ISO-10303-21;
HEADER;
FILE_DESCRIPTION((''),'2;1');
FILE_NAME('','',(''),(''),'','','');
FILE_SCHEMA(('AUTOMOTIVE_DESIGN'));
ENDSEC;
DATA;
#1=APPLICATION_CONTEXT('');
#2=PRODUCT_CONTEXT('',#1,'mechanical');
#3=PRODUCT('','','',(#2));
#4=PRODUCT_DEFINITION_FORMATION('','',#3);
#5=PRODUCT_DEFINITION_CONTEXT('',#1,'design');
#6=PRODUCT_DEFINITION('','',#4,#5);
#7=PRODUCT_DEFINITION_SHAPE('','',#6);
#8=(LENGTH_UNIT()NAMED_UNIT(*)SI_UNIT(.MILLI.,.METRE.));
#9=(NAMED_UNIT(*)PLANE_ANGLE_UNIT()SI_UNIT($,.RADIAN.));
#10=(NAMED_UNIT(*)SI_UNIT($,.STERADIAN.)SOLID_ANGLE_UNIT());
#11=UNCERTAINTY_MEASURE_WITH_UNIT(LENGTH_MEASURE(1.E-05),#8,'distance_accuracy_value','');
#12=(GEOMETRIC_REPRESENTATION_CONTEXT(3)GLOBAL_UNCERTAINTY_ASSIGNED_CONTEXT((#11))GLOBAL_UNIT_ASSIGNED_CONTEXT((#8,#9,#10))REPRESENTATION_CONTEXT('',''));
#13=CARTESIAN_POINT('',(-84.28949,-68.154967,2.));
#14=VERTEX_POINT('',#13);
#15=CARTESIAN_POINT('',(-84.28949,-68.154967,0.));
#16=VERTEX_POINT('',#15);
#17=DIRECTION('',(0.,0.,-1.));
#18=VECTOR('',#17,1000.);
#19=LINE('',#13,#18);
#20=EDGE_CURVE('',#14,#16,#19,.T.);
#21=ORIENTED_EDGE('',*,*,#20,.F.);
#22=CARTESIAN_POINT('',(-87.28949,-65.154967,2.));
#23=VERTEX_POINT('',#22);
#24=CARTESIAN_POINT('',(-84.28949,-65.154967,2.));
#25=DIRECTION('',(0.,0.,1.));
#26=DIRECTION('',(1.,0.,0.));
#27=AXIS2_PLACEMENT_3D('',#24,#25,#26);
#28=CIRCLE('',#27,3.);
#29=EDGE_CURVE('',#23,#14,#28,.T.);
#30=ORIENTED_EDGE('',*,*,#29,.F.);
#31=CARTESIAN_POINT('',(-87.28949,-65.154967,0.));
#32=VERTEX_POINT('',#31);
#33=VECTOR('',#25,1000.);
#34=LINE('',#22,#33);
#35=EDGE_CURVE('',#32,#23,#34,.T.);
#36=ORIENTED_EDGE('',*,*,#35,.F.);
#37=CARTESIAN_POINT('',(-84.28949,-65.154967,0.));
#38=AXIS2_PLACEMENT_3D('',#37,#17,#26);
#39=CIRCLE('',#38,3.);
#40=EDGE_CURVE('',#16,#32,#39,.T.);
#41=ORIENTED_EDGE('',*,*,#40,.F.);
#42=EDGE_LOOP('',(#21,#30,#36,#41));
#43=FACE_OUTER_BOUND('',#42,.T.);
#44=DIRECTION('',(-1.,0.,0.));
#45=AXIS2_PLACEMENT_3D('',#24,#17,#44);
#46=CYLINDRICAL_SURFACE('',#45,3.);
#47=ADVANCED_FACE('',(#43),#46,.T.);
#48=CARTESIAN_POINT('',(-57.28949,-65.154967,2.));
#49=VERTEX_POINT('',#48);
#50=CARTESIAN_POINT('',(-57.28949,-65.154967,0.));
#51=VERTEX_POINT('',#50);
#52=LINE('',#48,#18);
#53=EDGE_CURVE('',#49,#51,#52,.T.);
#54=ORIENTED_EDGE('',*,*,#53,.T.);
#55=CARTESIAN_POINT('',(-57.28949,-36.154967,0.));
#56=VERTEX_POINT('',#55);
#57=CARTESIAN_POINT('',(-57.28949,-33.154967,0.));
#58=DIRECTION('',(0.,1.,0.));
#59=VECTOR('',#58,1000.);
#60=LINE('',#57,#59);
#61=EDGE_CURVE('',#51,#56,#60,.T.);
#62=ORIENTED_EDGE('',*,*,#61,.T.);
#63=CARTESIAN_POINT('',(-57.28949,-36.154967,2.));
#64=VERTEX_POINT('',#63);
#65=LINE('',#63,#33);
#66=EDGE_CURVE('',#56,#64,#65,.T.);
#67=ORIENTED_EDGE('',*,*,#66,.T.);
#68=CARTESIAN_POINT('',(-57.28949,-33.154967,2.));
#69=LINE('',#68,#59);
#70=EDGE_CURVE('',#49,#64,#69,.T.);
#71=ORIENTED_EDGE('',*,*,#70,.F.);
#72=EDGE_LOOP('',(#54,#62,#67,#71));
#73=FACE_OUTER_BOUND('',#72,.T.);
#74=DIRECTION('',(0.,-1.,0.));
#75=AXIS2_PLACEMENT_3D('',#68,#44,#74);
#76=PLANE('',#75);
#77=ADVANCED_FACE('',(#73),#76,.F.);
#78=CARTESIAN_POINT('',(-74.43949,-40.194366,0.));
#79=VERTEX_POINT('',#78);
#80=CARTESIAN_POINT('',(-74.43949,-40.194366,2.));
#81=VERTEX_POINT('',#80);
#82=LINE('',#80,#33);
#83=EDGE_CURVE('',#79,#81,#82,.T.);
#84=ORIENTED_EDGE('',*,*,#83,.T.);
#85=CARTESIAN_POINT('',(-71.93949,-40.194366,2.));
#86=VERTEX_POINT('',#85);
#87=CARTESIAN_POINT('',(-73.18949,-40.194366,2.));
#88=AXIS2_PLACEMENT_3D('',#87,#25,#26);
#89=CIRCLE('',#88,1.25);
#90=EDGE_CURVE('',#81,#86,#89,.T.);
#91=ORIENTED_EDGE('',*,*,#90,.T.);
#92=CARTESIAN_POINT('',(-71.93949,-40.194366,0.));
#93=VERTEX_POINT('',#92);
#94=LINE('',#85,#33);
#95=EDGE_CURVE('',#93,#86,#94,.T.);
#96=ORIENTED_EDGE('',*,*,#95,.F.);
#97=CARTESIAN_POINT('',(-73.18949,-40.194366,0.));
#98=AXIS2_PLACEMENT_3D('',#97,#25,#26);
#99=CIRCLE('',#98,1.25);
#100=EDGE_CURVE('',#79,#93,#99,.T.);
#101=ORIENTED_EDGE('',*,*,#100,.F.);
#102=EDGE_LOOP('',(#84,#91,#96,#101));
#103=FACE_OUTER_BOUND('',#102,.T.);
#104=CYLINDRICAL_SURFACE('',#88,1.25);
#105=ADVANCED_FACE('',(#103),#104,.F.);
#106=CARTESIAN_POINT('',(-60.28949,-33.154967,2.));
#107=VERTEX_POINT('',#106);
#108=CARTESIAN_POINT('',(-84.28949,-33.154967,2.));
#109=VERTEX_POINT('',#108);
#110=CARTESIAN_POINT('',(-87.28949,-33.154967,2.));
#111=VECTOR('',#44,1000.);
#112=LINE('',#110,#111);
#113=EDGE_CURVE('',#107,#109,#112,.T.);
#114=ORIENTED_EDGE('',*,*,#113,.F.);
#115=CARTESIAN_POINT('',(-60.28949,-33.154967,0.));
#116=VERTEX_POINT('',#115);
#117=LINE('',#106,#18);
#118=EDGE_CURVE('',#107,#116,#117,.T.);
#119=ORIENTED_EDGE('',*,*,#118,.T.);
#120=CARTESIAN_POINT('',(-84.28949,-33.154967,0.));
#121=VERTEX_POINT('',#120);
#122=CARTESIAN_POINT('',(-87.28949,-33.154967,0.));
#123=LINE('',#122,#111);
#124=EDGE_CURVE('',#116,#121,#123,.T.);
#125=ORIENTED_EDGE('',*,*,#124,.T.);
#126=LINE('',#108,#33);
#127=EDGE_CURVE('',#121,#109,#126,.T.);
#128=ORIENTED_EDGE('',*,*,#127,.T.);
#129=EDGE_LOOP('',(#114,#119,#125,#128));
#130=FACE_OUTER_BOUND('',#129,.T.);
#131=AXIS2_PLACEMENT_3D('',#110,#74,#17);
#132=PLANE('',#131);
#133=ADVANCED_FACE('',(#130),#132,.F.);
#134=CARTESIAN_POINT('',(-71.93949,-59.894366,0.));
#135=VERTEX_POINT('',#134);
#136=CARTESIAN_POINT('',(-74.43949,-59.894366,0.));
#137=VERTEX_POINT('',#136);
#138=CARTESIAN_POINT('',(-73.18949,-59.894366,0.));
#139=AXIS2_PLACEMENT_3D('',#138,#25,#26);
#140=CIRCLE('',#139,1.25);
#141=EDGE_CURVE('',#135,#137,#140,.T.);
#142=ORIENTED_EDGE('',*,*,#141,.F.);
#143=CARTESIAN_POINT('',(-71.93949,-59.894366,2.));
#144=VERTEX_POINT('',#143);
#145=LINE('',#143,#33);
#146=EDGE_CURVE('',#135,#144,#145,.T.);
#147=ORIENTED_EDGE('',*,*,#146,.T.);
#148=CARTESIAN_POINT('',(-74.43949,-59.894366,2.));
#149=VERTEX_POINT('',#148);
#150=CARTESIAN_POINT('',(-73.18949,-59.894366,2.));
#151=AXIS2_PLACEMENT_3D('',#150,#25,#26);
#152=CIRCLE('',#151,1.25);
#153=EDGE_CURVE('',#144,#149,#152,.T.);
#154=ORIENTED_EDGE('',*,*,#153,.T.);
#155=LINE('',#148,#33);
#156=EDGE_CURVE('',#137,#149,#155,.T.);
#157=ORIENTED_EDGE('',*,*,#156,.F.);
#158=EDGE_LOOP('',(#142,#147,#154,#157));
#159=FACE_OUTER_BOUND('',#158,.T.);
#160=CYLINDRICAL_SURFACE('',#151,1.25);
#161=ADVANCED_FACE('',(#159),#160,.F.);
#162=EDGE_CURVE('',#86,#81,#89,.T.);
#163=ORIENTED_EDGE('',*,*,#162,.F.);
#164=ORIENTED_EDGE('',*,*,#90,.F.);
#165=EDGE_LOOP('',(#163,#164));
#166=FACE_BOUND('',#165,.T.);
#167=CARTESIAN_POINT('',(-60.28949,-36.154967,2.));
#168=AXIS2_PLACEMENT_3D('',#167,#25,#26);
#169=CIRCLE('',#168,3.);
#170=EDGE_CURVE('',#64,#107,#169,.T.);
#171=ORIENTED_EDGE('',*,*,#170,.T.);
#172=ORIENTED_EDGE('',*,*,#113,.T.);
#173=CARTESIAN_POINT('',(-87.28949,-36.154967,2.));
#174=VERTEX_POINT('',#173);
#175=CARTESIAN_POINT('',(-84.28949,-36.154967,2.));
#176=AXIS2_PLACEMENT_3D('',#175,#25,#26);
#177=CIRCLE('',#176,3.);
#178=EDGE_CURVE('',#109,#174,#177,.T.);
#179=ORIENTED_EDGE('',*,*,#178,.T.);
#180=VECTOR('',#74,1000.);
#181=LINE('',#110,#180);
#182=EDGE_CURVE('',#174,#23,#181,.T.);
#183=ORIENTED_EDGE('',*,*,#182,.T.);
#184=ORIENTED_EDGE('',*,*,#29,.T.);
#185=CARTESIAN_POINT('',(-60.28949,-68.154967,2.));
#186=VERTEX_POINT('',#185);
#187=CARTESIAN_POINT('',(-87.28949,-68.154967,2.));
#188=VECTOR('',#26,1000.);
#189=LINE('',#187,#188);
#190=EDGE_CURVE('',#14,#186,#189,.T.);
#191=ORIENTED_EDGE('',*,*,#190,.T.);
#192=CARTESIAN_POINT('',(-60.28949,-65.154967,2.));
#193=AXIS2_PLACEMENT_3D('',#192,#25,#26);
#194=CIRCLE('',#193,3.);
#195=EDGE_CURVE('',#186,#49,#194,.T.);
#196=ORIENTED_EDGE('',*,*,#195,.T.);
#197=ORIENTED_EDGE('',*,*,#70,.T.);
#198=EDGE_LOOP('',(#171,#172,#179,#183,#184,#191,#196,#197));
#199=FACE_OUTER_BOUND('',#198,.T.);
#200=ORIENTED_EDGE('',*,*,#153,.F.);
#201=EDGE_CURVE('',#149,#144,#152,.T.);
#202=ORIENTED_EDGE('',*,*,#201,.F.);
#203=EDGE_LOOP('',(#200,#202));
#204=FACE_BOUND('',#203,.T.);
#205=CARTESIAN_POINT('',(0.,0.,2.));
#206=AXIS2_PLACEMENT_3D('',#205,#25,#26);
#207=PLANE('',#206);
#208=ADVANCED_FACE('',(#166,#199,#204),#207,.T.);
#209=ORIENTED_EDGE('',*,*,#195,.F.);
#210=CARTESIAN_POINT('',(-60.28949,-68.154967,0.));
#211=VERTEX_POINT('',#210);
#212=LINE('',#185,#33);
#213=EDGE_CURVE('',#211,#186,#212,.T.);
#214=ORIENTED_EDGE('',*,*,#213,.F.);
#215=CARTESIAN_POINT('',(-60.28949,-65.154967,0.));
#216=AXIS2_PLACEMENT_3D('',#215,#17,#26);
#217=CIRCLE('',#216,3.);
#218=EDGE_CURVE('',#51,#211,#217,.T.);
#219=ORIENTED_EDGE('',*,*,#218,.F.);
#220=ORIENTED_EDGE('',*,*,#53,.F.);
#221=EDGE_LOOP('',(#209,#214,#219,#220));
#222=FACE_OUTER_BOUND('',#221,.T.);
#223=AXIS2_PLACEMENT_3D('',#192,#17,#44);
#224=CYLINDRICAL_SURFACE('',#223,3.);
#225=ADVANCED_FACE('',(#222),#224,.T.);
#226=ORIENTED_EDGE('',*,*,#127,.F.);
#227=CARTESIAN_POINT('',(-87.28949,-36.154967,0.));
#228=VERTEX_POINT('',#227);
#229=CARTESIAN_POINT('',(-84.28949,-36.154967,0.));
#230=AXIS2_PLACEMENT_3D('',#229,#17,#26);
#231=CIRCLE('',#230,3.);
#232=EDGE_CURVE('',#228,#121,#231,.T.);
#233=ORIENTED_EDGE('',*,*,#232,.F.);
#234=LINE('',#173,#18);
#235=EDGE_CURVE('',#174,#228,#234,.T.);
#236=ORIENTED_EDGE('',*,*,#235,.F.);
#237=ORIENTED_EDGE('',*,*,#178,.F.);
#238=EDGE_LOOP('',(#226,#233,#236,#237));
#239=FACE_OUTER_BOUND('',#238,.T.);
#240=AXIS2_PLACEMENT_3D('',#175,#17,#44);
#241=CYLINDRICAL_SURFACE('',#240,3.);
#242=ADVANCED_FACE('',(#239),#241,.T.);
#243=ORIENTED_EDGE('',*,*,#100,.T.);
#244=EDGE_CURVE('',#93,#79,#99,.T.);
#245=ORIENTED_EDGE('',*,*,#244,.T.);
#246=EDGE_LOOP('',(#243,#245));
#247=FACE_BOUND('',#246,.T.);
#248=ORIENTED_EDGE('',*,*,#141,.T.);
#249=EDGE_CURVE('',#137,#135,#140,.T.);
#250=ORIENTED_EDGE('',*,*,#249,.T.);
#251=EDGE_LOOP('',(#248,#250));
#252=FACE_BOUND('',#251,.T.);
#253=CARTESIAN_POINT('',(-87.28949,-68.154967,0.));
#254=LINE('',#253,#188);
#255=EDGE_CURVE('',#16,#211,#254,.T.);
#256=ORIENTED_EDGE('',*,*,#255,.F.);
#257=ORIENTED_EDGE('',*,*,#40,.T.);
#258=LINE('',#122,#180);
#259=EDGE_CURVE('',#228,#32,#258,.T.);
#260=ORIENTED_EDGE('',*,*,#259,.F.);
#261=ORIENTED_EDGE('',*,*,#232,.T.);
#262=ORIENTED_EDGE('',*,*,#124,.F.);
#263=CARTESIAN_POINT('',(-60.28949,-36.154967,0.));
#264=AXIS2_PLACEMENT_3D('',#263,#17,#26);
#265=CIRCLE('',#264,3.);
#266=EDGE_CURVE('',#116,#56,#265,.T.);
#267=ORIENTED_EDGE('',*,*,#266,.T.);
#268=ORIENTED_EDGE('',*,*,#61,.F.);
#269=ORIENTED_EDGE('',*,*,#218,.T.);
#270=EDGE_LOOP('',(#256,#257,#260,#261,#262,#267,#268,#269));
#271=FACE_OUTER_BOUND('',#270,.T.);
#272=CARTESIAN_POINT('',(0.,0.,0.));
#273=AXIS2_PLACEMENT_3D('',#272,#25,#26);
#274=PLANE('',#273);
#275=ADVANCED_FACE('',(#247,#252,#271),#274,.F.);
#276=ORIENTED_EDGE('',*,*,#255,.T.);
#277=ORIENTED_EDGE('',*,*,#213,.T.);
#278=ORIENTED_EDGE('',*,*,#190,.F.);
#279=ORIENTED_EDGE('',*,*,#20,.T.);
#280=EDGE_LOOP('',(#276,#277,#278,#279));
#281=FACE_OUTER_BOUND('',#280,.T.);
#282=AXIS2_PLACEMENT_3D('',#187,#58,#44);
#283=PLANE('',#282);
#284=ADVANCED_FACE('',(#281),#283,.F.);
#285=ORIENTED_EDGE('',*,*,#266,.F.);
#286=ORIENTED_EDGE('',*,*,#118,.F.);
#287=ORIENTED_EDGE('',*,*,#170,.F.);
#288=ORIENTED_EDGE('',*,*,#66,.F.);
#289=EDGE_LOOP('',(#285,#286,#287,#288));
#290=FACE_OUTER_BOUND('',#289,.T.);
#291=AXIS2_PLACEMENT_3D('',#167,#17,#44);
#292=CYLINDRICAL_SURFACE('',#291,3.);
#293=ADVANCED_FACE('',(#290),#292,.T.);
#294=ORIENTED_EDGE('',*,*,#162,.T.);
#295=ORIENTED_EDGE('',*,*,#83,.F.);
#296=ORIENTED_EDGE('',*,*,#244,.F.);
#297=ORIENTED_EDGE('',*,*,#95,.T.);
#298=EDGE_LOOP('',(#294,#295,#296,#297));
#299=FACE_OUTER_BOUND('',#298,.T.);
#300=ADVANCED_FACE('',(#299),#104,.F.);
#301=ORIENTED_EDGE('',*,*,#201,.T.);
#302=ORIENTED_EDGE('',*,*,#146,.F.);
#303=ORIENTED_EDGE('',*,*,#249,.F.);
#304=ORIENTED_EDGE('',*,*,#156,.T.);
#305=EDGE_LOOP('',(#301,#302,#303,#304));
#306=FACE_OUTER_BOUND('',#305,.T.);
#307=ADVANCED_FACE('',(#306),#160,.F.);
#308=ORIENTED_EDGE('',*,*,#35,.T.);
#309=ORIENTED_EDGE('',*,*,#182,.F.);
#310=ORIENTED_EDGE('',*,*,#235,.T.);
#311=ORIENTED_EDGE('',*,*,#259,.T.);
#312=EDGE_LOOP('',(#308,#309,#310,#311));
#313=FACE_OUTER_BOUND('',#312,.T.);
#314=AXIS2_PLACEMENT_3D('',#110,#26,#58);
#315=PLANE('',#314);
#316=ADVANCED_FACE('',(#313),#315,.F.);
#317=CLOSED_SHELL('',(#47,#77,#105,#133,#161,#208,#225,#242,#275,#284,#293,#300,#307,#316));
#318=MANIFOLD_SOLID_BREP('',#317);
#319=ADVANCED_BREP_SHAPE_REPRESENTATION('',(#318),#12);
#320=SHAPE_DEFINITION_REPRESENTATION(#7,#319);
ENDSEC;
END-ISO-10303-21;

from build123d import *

# Parameters (mm, degrees)
SKETCH1_W           = 30
SKETCH1_H           = 35
BOSS_EXTRUDE1_DEPTH = 2
FILLET1_R           = 3
M3_TAPPED_HOLE1_D   = 2.5


with BuildPart() as part:
    # Sketch1 → Boss-Extrude1 (new body)
    with BuildSketch(Plane.XY):
        with Locations((-72.289490021, -50.654966575)):
            Rectangle(SKETCH1_W, SKETCH1_H)
    extrude(amount=BOSS_EXTRUDE1_DEPTH)

    # Fillet1
    fillet1_edges = [part.edges().sort_by_distance(p)[0] for p in [
        (-87.289490021, -33.154966575, 1),
        (-57.289490021, -33.154966575, 1),
        (-57.289490021, -68.154966575, 1),
        (-87.289490021, -68.154966575, 1),
    ]]
    fillet(fillet1_edges, radius=FILLET1_R)

    # M3 Tapped Hole1 (through all)
    with Locations(Plane.XY.offset(2)):
        with Locations((-73.189490021, -59.894365688), (-73.189490021, -40.194365688)):
            Hole(M3_TAPPED_HOLE1_D / 2)


solid = part.part
